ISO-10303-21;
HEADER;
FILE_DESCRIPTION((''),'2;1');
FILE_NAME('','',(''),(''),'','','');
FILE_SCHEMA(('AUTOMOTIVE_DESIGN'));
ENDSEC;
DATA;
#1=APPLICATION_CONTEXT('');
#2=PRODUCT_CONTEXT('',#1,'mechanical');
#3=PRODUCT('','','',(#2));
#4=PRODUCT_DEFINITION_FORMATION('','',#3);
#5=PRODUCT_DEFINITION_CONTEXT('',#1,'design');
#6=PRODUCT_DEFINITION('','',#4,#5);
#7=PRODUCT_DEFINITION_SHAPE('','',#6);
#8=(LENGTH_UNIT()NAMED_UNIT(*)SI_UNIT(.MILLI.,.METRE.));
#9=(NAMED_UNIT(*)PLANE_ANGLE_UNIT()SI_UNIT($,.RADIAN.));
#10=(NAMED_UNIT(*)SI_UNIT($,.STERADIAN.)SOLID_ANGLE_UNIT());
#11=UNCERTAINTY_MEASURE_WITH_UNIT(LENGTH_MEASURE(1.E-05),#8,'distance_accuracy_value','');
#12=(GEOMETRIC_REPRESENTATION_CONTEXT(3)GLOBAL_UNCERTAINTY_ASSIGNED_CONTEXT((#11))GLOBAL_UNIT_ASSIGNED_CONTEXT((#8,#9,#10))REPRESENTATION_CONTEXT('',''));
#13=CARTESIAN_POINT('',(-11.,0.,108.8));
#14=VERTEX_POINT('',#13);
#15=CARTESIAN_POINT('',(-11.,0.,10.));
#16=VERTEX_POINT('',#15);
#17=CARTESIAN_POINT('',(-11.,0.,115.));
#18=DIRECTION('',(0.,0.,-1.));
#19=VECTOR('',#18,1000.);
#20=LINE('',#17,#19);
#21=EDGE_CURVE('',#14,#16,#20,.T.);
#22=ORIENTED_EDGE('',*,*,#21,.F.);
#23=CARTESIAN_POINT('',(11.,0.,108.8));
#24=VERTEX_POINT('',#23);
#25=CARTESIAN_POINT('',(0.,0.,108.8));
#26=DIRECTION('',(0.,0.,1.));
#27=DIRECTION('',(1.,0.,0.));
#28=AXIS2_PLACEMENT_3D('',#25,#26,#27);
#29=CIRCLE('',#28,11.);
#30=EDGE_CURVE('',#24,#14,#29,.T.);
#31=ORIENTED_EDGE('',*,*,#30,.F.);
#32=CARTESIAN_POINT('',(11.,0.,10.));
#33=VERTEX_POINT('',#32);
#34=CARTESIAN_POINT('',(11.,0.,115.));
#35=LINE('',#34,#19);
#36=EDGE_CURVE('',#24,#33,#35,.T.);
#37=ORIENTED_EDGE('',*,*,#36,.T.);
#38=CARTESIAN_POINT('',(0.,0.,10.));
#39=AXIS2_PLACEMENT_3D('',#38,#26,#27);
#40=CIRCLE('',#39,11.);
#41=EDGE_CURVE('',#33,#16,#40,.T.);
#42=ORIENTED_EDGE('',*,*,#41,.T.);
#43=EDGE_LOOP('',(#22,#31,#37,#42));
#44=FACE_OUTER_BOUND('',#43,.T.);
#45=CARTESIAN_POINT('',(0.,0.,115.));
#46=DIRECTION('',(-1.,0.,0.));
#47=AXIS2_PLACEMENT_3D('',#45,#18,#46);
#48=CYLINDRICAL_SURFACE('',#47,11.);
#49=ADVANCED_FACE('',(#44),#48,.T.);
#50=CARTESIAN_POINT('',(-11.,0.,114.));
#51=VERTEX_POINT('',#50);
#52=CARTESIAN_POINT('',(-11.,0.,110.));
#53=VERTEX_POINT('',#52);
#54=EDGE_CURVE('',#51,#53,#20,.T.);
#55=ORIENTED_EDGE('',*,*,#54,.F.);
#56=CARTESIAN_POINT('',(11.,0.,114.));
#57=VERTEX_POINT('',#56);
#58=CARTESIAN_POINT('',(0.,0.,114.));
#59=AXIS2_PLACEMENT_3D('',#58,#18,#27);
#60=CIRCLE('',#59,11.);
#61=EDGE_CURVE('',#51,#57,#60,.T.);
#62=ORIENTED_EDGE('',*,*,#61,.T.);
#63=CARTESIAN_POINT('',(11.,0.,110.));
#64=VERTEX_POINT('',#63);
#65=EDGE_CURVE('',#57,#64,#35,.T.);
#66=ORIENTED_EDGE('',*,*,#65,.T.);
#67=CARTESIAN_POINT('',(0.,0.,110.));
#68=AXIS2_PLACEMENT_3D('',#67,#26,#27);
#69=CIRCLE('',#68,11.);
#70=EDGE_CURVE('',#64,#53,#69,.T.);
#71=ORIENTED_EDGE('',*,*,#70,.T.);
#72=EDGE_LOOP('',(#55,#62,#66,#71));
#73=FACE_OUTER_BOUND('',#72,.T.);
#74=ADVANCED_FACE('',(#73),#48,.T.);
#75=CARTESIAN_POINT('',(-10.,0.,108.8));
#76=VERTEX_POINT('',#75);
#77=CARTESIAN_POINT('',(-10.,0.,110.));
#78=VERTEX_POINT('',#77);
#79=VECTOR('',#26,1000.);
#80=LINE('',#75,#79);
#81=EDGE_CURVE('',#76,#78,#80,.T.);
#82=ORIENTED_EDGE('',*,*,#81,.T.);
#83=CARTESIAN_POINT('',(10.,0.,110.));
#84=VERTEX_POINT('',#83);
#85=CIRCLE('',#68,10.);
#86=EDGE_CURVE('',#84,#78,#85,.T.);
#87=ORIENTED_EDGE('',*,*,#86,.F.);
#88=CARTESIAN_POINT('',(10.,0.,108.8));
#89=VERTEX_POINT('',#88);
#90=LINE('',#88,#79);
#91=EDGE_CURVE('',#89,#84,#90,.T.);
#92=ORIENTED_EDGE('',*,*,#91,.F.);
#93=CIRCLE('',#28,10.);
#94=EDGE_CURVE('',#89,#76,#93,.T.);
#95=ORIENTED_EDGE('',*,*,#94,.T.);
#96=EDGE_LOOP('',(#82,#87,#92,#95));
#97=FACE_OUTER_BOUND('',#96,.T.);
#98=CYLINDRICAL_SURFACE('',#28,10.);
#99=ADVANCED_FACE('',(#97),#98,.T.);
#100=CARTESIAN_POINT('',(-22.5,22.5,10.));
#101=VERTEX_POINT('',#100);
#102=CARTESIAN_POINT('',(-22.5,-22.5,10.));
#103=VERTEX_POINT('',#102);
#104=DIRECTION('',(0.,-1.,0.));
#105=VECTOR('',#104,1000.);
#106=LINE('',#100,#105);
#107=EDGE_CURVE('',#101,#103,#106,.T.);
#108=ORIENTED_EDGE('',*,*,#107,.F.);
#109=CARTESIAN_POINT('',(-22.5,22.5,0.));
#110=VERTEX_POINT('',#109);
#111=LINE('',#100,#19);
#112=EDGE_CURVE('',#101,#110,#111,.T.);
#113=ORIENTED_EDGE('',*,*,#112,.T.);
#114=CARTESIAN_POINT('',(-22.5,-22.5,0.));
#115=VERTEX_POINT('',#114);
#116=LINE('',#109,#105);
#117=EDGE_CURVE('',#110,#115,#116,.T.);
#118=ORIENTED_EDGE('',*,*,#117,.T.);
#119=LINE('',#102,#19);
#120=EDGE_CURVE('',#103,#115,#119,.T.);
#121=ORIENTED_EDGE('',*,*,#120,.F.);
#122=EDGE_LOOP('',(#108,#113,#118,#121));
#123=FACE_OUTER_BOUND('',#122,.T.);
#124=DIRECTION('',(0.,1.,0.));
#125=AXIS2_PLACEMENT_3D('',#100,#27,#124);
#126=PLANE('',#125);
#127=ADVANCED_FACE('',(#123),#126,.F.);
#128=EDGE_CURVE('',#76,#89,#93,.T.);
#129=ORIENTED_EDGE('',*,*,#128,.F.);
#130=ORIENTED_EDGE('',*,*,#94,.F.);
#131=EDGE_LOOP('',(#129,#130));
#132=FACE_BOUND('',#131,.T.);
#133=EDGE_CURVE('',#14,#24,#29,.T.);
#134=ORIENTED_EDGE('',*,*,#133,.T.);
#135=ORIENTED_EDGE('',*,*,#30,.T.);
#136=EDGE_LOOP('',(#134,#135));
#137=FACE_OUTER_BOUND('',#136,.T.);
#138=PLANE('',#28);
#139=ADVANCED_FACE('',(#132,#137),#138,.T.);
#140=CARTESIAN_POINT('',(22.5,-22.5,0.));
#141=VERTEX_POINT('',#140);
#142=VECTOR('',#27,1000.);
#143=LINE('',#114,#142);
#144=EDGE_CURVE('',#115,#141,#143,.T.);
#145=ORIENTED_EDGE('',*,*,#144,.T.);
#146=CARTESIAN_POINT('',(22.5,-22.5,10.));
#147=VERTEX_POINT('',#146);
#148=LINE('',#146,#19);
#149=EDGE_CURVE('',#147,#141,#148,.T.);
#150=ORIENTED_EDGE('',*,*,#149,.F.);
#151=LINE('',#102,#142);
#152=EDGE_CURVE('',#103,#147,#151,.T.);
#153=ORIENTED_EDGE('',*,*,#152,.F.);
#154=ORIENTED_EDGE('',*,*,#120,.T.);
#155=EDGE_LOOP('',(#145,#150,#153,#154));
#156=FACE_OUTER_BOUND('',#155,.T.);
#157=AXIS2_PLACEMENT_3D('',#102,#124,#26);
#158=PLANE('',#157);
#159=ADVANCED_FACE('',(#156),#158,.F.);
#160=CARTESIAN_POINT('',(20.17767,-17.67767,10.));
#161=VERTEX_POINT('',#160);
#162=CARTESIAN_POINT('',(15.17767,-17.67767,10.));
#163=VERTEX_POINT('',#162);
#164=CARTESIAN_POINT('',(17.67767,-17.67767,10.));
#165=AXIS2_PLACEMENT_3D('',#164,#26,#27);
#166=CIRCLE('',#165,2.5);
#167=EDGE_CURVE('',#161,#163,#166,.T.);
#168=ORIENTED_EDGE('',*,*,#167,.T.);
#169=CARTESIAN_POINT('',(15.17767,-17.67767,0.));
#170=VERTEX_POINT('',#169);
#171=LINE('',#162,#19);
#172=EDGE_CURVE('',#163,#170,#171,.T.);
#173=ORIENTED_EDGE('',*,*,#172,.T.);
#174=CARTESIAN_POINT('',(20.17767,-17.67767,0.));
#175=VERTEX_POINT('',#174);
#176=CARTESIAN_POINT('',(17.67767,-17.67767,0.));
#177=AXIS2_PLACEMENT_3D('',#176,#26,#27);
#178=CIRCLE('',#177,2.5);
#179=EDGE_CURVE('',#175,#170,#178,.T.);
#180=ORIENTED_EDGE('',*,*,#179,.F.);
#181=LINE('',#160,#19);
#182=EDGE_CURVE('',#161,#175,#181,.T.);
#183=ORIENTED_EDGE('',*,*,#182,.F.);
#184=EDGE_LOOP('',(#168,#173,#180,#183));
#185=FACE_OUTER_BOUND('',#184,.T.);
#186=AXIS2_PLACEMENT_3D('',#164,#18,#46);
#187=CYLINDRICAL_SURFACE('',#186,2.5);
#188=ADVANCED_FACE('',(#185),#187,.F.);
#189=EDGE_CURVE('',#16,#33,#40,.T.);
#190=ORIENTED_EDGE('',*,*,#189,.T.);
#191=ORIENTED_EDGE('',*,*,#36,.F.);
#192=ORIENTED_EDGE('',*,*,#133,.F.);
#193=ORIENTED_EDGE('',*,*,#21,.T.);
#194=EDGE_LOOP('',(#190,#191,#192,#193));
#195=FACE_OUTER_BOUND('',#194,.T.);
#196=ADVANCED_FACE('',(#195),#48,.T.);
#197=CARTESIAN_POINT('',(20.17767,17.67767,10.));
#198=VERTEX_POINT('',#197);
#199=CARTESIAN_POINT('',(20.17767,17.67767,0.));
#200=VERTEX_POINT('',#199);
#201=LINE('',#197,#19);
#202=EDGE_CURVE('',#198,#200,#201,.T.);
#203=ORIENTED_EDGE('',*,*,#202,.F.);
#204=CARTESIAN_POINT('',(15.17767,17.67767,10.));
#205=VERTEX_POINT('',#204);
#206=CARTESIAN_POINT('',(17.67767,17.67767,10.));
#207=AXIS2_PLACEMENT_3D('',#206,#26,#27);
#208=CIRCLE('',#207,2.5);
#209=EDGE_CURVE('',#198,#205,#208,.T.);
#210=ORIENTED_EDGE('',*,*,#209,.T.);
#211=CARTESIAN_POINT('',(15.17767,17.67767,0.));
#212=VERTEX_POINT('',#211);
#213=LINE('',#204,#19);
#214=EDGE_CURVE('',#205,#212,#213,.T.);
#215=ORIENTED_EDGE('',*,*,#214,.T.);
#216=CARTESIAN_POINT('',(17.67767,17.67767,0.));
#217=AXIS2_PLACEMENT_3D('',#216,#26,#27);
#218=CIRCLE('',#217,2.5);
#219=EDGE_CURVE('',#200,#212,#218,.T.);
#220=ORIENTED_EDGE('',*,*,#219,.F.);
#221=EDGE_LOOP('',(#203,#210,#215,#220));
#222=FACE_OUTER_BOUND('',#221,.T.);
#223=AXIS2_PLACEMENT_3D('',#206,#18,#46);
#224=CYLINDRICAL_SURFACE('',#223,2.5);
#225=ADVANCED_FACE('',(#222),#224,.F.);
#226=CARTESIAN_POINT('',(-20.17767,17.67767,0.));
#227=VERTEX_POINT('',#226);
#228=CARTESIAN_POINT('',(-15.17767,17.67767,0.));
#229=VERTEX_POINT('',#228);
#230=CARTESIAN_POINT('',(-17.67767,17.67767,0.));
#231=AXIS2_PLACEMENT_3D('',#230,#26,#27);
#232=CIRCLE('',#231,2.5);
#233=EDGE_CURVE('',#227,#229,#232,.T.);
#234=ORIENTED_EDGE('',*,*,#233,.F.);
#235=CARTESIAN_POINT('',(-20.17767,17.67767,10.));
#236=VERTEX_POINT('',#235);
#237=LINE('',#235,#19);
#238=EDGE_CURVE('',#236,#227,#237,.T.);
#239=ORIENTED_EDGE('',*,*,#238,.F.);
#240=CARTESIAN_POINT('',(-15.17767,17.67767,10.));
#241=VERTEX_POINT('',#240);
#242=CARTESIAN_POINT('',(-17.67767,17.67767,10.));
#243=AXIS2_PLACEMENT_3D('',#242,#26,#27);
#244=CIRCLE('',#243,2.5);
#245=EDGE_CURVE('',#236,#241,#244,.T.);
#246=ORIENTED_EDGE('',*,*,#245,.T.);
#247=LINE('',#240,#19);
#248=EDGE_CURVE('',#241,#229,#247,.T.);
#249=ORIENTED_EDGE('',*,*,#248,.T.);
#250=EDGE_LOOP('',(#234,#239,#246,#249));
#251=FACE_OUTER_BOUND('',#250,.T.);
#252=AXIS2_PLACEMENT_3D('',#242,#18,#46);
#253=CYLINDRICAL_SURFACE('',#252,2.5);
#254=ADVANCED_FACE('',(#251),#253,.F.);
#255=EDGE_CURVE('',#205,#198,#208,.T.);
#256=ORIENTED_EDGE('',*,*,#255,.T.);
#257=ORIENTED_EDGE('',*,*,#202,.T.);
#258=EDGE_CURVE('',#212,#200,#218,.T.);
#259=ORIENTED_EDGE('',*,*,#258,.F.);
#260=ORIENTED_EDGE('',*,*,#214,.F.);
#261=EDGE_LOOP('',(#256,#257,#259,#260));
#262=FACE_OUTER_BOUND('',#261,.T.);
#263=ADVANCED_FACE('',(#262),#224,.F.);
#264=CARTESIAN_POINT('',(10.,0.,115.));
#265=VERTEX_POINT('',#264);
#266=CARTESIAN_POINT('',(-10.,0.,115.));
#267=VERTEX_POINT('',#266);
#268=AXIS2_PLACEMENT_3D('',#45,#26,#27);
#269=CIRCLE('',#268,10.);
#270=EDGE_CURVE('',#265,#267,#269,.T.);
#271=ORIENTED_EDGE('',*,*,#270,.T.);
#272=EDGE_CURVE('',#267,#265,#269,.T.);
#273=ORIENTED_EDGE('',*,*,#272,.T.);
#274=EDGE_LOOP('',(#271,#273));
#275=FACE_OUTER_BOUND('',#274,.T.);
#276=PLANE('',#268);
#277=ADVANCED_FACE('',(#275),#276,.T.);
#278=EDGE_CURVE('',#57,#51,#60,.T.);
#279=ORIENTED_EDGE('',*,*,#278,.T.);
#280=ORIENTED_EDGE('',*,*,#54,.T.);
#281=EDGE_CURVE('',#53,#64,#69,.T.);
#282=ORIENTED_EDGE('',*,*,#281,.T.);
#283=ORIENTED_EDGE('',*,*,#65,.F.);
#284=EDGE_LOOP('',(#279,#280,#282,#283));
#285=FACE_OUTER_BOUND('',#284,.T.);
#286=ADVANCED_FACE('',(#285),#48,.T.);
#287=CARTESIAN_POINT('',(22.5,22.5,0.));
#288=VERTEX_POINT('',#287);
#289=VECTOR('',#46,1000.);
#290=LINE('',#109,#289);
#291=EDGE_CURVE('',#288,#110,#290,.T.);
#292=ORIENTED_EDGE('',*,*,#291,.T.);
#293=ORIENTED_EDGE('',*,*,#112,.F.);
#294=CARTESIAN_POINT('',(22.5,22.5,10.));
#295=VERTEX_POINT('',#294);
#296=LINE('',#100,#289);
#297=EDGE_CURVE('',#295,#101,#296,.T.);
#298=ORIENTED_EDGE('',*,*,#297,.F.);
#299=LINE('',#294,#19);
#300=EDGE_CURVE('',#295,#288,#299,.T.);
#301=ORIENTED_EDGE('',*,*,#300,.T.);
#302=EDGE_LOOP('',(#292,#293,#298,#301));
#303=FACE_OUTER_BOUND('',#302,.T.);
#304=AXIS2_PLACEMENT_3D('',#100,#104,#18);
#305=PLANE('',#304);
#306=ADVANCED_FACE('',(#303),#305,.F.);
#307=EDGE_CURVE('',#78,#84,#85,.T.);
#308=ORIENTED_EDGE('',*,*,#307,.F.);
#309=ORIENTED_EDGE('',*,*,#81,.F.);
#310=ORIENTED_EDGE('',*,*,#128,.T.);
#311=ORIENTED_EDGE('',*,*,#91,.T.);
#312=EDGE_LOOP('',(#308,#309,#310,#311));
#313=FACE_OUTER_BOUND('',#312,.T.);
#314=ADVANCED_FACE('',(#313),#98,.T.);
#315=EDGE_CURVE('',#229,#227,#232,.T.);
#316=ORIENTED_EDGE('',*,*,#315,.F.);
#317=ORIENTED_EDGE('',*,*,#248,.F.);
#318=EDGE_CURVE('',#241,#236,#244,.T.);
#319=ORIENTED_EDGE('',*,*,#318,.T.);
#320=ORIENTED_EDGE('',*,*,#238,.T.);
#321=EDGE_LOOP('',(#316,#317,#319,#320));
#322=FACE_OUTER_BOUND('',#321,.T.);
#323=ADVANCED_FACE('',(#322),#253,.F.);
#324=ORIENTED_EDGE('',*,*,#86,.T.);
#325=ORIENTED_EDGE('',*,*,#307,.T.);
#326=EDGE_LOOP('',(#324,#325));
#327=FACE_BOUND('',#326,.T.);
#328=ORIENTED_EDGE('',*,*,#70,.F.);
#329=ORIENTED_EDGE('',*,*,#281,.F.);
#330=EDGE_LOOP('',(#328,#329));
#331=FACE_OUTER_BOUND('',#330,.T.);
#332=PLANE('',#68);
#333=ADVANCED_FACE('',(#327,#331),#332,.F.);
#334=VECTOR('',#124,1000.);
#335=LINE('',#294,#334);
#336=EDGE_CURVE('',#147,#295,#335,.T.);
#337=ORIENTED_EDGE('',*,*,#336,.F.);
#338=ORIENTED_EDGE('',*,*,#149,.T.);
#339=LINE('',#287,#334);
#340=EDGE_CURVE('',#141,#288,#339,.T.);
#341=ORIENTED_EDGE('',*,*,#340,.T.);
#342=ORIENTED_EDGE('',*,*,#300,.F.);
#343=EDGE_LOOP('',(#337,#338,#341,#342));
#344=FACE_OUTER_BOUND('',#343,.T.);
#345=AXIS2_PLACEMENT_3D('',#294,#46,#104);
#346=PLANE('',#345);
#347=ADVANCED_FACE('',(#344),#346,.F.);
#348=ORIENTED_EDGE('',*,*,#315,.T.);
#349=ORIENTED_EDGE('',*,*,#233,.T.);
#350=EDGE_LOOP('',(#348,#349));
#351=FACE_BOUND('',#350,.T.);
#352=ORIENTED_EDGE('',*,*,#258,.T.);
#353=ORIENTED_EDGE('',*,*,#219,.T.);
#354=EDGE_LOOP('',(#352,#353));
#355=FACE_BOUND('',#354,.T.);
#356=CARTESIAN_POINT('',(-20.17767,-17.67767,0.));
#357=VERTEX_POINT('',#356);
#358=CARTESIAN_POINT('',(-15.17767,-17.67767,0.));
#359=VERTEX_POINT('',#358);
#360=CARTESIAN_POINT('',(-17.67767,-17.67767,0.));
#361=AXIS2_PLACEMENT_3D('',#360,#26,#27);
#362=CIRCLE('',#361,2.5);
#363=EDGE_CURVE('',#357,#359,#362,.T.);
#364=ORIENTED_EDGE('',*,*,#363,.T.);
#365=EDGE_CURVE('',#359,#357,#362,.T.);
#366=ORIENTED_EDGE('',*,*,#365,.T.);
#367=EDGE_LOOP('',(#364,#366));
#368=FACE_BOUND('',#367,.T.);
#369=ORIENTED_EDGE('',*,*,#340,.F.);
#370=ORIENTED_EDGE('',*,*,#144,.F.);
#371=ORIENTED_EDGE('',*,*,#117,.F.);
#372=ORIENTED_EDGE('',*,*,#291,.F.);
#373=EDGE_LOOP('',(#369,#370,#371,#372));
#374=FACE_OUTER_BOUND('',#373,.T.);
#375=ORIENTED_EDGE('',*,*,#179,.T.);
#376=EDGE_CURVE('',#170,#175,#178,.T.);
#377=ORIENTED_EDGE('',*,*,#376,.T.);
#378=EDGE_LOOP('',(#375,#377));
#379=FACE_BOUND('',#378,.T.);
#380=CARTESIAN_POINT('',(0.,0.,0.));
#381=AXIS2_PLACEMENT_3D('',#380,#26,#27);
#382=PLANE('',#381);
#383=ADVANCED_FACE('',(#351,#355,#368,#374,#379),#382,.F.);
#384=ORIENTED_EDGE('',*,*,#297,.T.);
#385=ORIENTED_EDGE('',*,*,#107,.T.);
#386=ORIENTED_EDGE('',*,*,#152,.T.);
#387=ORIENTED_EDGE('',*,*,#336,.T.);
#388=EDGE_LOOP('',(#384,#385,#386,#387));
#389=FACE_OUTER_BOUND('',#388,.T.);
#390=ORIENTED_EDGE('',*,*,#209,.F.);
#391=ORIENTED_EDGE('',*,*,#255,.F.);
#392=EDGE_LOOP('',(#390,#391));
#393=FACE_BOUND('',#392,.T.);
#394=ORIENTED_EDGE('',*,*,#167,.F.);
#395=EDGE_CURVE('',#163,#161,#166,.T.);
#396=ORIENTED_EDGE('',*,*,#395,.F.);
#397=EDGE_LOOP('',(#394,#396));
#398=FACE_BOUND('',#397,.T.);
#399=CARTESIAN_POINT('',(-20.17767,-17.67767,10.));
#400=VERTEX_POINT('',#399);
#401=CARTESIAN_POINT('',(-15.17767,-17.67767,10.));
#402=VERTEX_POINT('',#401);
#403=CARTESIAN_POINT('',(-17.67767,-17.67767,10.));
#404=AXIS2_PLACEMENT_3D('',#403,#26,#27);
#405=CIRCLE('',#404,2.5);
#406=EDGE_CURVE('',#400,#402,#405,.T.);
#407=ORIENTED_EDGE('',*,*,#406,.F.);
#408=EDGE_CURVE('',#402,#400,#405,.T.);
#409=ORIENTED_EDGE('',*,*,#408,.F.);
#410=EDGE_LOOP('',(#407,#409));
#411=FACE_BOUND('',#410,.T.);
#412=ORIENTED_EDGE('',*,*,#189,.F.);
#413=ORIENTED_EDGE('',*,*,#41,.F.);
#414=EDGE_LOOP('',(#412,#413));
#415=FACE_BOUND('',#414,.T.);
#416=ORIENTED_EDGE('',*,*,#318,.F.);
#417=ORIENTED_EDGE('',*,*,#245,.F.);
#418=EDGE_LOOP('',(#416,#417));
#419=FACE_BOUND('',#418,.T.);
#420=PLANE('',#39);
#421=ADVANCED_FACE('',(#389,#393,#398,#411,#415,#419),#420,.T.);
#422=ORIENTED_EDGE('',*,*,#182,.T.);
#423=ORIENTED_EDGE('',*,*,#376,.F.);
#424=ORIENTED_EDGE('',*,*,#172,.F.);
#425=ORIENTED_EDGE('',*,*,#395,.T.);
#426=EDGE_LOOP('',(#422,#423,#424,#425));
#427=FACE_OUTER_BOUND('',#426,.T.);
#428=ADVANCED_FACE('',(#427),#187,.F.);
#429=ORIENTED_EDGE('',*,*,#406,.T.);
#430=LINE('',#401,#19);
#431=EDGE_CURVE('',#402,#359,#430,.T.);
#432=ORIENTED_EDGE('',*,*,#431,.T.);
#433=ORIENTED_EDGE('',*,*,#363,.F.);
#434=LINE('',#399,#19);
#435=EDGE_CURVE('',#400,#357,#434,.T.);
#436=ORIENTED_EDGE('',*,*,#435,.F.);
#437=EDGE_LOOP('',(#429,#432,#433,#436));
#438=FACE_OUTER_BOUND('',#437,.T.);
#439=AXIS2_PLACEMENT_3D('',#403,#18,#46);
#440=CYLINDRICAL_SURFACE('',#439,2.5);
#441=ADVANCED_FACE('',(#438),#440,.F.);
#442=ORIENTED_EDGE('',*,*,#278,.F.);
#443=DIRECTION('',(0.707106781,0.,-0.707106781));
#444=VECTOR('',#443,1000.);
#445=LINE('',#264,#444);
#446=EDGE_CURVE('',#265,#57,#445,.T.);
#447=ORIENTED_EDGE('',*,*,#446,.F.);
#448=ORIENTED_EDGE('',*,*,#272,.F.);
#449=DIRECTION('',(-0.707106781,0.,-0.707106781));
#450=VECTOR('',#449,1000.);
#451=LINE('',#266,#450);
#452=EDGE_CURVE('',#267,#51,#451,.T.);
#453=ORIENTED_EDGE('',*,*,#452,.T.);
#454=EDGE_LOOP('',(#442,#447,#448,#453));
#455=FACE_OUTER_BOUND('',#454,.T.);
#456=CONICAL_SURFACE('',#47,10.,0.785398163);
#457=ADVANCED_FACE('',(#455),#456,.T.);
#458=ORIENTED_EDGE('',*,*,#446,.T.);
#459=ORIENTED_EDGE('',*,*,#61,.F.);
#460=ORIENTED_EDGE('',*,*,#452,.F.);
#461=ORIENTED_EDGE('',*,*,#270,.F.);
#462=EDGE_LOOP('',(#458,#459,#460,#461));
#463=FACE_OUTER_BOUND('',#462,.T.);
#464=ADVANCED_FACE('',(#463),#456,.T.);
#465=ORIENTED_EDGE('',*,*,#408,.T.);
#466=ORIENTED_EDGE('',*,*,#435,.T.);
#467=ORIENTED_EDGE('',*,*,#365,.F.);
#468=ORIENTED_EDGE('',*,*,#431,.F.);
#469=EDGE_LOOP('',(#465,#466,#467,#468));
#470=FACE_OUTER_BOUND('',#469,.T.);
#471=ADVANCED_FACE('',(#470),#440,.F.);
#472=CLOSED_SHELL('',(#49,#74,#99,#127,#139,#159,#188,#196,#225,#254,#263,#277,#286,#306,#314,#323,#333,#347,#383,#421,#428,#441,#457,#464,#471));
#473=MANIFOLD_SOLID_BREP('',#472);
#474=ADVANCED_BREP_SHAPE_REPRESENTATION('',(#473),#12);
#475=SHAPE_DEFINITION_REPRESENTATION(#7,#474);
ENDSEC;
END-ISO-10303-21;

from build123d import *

# Parameters (mm, degrees)
SKETCH1_W           = 45
SKETCH1_H           = 45
SKETCH1_R           = 2.5
BOSS_EXTRUDE1_DEPTH = 10
SKETCH2_R           = 11
BOSS_EXTRUDE2_DEPTH = 105
CHAMFER1_SIZE       = 1
CUT_EXTRUDE1_START  = -5
SKETCH3_R           = 12.248377089
SKETCH3_R_2         = 10
CUT_EXTRUDE1_DEPTH  = 1.2


with BuildPart() as part:
    # Sketch1 → Boss-Extrude1 (new body)
    with BuildSketch(Plane.XY):
        Rectangle(SKETCH1_W, SKETCH1_H)
        with Locations((17.67766953, 17.67766953)):
            Circle(SKETCH1_R, mode=Mode.SUBTRACT)
        with Locations((17.67766953, -17.67766953)):
            Circle(SKETCH1_R, mode=Mode.SUBTRACT)
        with Locations((-17.67766953, -17.67766953)):
            Circle(SKETCH1_R, mode=Mode.SUBTRACT)
        with Locations((-17.67766953, 17.67766953)):
            Circle(SKETCH1_R, mode=Mode.SUBTRACT)
    extrude(amount=BOSS_EXTRUDE1_DEPTH)

    # Sketch2 → Boss-Extrude2 (add)
    with BuildSketch(Plane.XY.offset(10)):
        Circle(SKETCH2_R)
    extrude(amount=BOSS_EXTRUDE2_DEPTH)

    # Chamfer1
    chamfer1_edges = [part.edges().sort_by_distance(p)[0] for p in [
        (-11, 0, 115),
    ]]
    chamfer(chamfer1_edges, length=CHAMFER1_SIZE)

    # Sketch3 → Cut-Extrude1 (cut)
    with BuildSketch(Plane.XY.offset(115).offset(CUT_EXTRUDE1_START)):
        Circle(SKETCH3_R)
        Circle(SKETCH3_R_2, mode=Mode.SUBTRACT)
    extrude(amount=-CUT_EXTRUDE1_DEPTH, mode=Mode.SUBTRACT)


solid = part.part
